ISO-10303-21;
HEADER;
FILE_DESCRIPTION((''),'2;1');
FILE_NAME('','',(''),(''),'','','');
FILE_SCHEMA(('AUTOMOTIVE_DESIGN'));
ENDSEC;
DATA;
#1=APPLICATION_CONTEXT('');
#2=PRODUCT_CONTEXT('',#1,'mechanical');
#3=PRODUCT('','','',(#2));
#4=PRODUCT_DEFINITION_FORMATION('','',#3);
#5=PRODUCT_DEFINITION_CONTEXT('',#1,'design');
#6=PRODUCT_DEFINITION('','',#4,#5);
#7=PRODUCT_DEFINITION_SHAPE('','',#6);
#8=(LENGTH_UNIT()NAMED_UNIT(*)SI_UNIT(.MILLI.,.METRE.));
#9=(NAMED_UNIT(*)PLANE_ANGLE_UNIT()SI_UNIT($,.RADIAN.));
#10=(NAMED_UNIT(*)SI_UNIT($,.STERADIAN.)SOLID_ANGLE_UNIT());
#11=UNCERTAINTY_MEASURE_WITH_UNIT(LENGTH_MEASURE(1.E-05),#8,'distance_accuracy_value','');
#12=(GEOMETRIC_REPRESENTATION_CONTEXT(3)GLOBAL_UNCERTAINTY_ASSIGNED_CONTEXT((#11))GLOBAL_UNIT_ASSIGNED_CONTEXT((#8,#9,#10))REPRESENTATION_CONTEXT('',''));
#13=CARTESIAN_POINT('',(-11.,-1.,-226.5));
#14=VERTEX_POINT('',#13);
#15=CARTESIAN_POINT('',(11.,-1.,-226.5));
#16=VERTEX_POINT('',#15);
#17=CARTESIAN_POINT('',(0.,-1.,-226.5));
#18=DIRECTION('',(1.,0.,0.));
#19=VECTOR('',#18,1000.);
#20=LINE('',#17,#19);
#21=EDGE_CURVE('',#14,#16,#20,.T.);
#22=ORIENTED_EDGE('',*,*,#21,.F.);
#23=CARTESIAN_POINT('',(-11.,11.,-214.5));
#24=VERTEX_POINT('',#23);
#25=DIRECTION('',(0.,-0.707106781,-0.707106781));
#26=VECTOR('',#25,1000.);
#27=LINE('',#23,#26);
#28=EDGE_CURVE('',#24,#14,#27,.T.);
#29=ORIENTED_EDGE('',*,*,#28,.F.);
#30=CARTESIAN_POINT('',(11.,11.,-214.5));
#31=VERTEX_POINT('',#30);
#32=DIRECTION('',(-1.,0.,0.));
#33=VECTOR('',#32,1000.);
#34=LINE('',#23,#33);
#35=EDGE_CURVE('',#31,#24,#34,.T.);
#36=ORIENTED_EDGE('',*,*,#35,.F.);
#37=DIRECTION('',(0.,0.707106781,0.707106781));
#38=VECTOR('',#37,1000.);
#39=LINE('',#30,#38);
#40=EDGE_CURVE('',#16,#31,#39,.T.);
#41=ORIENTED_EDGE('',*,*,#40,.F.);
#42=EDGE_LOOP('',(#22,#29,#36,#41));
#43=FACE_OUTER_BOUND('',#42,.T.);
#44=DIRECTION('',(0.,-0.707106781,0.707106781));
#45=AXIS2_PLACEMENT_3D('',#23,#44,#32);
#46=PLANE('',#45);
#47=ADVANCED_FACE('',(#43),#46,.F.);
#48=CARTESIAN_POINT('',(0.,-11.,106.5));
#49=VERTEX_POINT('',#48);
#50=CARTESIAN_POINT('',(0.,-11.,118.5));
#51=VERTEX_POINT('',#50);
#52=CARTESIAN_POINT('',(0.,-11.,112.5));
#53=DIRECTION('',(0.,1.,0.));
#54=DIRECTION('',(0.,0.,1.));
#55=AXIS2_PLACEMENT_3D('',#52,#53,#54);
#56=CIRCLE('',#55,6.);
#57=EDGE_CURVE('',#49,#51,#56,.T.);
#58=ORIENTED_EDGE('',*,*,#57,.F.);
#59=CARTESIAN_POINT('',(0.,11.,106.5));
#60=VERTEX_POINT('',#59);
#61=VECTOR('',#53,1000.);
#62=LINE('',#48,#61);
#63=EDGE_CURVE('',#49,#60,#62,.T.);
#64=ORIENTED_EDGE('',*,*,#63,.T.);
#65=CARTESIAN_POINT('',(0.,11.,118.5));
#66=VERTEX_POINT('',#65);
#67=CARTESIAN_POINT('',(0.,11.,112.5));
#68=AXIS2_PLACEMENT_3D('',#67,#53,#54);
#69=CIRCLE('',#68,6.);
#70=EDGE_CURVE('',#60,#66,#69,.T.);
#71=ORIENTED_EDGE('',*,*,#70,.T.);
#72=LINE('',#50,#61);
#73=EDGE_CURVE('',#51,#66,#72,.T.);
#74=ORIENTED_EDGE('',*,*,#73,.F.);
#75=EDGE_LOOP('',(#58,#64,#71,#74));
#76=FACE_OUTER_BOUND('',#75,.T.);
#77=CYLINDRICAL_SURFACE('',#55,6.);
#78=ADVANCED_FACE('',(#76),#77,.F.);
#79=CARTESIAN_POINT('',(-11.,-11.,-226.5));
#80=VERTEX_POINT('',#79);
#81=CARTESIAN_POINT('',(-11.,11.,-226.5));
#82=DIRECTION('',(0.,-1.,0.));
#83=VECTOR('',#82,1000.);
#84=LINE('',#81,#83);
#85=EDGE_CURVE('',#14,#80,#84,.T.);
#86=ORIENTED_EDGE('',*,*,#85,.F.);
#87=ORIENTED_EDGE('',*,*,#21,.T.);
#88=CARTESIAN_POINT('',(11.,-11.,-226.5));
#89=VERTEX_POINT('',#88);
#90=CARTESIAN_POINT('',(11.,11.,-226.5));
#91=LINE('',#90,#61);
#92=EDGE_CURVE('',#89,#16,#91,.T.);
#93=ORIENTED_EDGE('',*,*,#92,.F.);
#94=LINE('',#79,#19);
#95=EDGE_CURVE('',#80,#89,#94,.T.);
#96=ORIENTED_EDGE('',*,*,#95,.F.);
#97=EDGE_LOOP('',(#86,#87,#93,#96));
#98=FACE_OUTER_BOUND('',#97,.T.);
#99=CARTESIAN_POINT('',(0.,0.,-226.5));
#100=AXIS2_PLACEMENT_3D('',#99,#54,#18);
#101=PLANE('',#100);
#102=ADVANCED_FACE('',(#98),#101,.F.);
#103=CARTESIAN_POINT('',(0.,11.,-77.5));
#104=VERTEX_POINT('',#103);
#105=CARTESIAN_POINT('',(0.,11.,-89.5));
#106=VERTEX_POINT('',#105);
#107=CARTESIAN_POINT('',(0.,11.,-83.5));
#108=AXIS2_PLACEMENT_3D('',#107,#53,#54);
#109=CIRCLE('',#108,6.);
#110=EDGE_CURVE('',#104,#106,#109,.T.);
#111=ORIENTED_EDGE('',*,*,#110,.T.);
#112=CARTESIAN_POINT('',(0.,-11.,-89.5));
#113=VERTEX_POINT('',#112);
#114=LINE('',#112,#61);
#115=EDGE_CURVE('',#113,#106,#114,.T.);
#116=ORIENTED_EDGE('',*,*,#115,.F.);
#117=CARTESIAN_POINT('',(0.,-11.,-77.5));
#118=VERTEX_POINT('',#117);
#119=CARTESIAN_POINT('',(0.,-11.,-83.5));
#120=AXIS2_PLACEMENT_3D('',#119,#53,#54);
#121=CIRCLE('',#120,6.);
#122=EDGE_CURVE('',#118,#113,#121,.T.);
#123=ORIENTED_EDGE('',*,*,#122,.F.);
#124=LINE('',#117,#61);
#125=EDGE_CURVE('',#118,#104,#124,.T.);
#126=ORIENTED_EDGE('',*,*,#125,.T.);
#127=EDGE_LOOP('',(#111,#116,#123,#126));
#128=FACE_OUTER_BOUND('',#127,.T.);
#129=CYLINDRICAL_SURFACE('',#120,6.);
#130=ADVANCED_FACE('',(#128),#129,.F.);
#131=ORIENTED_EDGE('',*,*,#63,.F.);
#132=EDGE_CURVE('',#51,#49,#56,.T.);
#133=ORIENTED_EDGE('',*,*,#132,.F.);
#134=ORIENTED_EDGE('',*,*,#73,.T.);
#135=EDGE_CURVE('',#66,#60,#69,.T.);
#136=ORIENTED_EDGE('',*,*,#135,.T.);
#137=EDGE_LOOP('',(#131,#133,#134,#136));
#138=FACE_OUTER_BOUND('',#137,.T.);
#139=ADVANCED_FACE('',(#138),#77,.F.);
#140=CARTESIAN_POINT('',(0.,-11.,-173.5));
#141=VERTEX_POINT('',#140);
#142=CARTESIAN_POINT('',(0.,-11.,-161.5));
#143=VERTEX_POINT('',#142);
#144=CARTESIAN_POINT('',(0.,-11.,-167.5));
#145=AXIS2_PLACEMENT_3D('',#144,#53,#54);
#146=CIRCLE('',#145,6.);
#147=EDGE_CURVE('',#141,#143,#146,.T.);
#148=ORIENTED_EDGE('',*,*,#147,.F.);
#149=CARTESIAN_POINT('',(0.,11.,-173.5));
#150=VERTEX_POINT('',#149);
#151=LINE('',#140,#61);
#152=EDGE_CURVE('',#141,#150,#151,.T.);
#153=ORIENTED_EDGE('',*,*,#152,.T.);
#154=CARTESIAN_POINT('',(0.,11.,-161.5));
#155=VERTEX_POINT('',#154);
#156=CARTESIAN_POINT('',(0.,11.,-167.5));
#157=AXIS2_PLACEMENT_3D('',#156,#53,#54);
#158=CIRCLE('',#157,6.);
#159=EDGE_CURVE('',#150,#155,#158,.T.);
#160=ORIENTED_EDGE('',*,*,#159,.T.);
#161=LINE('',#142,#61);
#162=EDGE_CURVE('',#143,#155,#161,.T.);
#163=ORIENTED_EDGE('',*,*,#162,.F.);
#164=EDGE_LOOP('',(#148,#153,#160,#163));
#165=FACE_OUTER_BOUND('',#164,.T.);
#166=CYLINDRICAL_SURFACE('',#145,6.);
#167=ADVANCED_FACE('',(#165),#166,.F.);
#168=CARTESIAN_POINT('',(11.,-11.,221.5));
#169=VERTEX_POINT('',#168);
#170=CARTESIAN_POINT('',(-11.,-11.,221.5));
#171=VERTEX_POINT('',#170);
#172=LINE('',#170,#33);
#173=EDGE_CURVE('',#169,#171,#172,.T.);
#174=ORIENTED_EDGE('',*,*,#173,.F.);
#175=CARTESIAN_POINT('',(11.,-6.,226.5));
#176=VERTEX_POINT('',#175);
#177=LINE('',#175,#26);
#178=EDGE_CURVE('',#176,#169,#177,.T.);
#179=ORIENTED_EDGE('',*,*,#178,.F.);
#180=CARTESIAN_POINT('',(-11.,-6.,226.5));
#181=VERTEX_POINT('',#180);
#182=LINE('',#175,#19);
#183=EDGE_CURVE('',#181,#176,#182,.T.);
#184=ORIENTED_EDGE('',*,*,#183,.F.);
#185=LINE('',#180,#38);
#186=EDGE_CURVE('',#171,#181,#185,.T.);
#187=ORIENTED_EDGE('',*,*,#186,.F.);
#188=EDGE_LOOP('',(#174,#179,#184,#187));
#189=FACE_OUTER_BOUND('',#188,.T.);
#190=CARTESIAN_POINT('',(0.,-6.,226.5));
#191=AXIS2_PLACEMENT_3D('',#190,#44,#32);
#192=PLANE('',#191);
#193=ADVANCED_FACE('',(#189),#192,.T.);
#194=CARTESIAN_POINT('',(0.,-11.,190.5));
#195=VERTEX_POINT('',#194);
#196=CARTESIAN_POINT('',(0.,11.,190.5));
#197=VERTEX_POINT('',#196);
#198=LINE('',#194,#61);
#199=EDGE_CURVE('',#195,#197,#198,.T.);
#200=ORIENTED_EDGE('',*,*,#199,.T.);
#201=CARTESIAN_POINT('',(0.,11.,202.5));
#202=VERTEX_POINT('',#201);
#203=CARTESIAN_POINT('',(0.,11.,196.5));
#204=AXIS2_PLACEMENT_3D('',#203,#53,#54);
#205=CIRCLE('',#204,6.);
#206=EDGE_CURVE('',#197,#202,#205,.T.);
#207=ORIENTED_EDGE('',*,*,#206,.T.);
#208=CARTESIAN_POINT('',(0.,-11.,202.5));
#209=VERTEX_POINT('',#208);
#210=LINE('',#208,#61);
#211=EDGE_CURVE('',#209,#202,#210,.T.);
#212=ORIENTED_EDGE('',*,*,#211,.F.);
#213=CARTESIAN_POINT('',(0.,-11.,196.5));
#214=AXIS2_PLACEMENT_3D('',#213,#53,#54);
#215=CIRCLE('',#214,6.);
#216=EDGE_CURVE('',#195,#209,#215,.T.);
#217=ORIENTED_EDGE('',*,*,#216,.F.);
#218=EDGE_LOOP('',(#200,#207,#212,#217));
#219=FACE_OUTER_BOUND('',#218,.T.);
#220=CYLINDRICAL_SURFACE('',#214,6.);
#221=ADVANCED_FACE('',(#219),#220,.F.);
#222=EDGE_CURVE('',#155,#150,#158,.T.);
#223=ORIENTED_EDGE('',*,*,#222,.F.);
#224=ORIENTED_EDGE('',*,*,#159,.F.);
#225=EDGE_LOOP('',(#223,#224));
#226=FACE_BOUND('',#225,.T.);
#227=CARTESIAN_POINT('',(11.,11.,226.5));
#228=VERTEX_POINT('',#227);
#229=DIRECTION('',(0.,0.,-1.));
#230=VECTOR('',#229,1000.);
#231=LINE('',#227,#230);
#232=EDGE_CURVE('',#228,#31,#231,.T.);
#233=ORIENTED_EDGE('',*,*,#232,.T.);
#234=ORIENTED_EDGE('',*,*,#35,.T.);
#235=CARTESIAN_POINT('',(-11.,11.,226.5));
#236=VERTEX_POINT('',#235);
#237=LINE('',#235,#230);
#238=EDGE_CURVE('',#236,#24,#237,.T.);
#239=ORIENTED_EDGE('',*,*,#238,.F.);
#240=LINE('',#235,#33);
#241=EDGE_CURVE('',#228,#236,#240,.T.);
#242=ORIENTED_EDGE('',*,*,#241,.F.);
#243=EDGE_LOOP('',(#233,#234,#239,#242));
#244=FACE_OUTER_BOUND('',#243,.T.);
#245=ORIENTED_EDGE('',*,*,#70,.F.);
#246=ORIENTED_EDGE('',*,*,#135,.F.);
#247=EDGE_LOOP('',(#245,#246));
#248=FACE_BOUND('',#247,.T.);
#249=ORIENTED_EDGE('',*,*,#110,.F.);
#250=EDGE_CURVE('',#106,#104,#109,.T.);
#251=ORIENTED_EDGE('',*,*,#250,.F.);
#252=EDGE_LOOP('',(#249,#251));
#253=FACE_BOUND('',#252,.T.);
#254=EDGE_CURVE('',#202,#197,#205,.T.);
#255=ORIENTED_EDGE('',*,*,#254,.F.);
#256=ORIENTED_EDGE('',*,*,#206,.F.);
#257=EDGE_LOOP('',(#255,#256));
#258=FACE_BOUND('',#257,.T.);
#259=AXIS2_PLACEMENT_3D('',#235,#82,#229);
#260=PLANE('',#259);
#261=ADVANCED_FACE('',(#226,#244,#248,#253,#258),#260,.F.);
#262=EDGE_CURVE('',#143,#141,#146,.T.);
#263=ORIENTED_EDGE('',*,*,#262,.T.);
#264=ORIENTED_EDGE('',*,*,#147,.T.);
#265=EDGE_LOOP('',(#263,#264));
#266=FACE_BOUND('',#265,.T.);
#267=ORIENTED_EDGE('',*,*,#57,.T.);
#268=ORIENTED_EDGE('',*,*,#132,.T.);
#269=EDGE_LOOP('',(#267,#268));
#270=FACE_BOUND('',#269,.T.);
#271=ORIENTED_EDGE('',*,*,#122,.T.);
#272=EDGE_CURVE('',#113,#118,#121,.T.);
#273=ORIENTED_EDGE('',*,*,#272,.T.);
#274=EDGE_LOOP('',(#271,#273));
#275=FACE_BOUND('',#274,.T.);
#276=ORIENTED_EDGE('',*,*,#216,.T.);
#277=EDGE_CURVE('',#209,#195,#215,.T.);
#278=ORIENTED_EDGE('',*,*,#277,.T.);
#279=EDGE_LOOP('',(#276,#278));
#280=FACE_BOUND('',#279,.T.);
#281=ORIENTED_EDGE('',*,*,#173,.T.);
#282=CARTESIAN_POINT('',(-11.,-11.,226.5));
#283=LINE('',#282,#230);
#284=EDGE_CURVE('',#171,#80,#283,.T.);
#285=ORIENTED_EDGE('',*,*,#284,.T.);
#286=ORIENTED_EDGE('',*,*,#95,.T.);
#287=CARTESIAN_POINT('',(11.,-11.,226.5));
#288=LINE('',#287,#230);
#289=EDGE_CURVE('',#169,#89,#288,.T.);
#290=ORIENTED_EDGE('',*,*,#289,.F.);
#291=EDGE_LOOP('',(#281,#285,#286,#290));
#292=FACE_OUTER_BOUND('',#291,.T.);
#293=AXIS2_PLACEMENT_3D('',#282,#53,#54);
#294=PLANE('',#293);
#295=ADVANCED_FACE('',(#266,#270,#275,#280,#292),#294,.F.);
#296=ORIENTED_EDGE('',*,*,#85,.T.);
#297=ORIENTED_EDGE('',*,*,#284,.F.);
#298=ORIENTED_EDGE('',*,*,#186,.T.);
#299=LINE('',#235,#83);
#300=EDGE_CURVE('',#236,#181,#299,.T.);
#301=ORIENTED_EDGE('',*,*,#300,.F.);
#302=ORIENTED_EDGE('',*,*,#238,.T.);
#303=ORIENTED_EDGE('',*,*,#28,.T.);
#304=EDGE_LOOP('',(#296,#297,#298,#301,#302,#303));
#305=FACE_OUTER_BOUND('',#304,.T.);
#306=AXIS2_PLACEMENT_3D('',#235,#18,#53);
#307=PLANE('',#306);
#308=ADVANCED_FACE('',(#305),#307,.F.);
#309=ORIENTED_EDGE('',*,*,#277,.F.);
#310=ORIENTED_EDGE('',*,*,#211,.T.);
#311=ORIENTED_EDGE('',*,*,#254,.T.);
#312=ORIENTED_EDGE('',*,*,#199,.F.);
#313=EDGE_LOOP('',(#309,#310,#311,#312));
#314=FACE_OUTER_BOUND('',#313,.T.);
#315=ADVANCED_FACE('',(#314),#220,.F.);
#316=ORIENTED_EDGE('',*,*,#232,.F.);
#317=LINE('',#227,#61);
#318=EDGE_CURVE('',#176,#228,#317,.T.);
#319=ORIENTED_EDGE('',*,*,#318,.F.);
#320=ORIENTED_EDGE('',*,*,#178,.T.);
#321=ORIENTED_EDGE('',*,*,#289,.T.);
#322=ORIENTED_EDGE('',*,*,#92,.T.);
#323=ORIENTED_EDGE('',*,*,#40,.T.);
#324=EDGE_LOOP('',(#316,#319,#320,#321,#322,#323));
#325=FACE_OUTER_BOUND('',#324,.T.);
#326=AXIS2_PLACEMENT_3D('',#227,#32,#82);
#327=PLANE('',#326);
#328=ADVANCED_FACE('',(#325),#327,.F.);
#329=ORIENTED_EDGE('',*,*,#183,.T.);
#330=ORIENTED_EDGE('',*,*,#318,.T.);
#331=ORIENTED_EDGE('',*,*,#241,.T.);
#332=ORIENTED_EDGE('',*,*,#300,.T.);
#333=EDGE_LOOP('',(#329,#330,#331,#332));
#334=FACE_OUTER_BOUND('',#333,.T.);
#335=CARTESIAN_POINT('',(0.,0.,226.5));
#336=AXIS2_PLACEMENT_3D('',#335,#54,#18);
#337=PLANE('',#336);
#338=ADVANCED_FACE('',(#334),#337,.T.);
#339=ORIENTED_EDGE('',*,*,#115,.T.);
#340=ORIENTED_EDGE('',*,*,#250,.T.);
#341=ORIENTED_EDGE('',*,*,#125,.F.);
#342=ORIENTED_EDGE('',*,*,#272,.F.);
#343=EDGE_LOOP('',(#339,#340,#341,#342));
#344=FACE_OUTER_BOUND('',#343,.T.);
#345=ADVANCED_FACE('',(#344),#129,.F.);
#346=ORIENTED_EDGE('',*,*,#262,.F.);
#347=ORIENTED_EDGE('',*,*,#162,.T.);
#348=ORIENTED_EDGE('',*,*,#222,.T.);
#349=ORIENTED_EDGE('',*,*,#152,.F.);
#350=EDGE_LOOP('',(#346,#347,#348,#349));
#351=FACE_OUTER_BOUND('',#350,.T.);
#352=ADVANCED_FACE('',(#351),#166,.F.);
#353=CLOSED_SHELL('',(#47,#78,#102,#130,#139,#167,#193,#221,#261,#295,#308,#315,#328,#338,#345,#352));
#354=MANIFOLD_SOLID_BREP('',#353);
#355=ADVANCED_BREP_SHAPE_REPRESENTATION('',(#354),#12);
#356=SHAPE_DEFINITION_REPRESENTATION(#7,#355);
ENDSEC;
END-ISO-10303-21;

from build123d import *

# Parameters (mm, degrees)
SKETCH1_W           = 22
SKETCH1_H           = 22
BOSS_EXTRUDE1_DEPTH = 226.5
SKETCH2_R           = 6
CUT_EXTRUDE1_DEPTH  = 228.831626426
CHAMFER1_SIZE       = 5
CHAMFER2_SIZE       = 12


with BuildPart() as part:
    # Sketch1 → Boss-Extrude1 (new, symmetric)
    with BuildSketch(Plane.XY):
        Rectangle(SKETCH1_W, SKETCH1_H)
    extrude(amount=BOSS_EXTRUDE1_DEPTH, both=True)

    # Sketch2 → Cut-Extrude1 (cut, through all)
    with BuildSketch(Plane(origin=(0, 11, 0), x_dir=(1, 0, 0), z_dir=(0, 1, 0))):
        with Locations(Location((0, -196.5, 0), (0, 0, 270))):
            Circle(SKETCH2_R)
        with Locations(Location((0, -112.5, 0), (0, 0, 270))):
            Circle(SKETCH2_R)
        with Locations(Location((0, 83.5, 0), (0, 0, 270))):
            Circle(SKETCH2_R)
        with Locations(Location((0, 167.5, 0), (0, 0, 270))):
            Circle(SKETCH2_R)
    extrude(amount=-CUT_EXTRUDE1_DEPTH, mode=Mode.SUBTRACT)

    # Chamfer1
    chamfer1_edges = [part.edges().sort_by_distance(p)[0] for p in [
        (0, -11, 226.5),
    ]]
    chamfer(chamfer1_edges, length=CHAMFER1_SIZE)

    # Chamfer2
    chamfer2_edges = [part.edges().sort_by_distance(p)[0] for p in [
        (0, 11, -226.5),
    ]]
    chamfer(chamfer2_edges, length=CHAMFER2_SIZE)


solid = part.part
